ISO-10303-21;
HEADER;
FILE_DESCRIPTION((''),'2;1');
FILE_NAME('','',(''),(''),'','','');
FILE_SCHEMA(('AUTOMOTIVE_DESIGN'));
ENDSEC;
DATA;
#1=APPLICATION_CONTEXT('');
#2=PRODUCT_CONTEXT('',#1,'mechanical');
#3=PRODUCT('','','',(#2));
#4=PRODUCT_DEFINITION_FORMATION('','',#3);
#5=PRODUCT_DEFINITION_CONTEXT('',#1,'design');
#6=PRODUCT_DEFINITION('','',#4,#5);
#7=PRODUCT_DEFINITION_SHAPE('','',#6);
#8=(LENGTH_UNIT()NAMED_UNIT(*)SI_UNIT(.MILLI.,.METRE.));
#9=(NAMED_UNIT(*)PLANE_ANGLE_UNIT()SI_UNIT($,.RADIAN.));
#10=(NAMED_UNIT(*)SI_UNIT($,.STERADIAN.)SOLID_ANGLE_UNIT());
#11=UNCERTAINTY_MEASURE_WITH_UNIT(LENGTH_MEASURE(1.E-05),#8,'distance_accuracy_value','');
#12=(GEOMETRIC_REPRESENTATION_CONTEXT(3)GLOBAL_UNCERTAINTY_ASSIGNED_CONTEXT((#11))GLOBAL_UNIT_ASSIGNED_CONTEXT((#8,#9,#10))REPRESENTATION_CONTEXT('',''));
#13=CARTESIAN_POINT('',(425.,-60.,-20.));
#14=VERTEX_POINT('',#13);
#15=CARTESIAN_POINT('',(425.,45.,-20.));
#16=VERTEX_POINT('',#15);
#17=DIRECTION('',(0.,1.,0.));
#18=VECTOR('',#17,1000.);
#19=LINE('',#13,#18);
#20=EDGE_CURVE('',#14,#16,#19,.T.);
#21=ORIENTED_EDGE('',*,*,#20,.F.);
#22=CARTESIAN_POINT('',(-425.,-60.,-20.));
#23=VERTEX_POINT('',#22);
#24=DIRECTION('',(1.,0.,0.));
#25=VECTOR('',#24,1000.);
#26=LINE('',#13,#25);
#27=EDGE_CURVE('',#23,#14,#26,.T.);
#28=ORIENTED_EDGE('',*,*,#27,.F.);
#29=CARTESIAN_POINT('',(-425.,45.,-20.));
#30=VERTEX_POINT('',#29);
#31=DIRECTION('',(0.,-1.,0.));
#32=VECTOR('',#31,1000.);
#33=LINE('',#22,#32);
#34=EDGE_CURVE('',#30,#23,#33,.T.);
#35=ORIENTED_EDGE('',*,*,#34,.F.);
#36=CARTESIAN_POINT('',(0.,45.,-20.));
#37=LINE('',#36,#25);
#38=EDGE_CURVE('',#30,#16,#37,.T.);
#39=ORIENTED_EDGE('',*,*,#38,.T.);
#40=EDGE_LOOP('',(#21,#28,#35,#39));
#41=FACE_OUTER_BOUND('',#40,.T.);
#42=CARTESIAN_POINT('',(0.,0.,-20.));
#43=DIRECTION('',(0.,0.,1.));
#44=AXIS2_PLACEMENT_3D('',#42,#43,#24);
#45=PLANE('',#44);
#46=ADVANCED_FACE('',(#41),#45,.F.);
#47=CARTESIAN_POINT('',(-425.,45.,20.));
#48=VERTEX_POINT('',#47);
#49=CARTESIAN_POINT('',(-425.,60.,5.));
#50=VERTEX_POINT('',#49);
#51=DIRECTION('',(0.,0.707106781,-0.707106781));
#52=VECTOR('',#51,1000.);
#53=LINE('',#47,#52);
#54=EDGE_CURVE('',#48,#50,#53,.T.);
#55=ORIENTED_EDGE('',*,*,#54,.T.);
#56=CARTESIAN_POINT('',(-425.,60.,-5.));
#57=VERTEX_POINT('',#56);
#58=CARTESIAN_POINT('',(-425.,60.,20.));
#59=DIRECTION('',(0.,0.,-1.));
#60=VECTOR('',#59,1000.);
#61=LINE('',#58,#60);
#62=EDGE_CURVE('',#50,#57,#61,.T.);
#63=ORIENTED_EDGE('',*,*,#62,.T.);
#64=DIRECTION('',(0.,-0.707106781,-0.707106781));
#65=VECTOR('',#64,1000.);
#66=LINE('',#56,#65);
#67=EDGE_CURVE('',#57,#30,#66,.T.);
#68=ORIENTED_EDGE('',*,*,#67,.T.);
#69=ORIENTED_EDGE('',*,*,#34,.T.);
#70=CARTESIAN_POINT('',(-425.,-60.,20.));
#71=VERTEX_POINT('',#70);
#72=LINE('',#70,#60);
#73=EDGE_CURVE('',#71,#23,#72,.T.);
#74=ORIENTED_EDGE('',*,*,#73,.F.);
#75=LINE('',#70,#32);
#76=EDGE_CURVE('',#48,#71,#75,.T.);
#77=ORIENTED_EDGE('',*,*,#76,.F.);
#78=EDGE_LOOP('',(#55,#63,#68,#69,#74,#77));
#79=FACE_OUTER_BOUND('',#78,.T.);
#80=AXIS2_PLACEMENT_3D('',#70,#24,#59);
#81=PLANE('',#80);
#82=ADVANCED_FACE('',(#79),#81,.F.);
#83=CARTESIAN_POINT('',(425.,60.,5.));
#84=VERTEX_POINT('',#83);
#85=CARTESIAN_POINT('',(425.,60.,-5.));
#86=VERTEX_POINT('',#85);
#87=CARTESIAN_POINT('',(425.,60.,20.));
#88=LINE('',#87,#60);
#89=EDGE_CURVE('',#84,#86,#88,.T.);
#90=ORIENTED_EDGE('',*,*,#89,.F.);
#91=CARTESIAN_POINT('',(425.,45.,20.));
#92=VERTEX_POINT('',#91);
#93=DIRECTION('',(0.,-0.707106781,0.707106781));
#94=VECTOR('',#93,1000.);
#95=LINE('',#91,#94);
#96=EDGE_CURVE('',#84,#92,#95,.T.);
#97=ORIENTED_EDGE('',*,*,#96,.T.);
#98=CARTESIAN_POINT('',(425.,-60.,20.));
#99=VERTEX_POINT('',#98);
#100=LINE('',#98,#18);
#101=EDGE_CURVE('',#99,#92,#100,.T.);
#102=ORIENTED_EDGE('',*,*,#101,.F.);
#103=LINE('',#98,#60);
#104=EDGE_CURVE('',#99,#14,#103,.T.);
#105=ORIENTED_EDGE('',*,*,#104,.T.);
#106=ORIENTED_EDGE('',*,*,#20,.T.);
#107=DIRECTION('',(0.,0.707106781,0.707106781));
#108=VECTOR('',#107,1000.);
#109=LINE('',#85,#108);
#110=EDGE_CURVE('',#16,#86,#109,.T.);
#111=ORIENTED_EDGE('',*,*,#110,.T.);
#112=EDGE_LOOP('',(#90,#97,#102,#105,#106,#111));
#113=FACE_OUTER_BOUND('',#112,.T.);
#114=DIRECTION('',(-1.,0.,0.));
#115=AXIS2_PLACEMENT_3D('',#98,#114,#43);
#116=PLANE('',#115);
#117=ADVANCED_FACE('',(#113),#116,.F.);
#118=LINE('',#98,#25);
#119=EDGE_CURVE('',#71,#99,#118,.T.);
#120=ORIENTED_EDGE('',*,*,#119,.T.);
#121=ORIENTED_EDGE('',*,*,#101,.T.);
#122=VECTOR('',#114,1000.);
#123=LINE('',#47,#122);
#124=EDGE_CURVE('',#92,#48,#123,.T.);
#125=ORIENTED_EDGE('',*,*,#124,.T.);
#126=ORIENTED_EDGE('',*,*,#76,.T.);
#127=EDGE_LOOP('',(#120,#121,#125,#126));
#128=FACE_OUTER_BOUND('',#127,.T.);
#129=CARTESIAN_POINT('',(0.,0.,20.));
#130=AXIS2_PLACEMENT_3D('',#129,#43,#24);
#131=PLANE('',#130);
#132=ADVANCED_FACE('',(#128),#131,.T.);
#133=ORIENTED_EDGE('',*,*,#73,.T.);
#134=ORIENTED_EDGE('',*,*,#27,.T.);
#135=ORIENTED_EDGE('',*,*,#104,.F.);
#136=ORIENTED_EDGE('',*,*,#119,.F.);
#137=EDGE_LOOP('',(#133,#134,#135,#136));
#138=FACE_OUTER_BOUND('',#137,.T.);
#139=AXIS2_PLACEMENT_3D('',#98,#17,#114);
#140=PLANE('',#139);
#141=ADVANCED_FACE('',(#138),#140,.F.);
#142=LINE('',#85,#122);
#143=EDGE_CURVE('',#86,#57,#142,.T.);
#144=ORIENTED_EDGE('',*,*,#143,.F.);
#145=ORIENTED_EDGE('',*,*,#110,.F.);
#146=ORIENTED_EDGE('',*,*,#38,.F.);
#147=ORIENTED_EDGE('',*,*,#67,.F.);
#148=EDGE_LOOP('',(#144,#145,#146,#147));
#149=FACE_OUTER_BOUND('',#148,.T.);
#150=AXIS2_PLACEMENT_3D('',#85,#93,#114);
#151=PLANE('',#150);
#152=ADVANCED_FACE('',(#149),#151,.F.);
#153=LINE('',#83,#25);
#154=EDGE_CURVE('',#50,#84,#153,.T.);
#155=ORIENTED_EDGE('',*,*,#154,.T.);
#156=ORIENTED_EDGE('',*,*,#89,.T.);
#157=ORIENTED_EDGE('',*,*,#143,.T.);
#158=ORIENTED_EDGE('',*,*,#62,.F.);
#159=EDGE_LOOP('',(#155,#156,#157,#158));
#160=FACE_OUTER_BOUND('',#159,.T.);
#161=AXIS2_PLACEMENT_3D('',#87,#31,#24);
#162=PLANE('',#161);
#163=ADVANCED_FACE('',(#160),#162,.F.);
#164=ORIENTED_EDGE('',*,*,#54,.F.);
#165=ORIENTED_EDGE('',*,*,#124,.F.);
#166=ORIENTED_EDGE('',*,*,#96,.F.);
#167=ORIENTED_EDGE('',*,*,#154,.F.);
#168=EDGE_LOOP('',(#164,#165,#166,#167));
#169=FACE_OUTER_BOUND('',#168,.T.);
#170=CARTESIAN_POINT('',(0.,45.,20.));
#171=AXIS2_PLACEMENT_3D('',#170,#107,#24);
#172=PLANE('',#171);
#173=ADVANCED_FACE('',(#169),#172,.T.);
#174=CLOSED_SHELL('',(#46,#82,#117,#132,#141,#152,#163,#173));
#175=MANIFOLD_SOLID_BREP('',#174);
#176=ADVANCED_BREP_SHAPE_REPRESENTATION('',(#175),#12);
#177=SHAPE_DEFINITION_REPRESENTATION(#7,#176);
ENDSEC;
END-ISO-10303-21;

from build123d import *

# Parameters (mm, degrees)
SKETCH1_W           = 850
SKETCH1_H           = 120
BOSS_EXTRUDE1_DEPTH = 20
CHAMFER1_SIZE       = 15


with BuildPart() as part:
    # Sketch1 → Boss-Extrude1 (new, symmetric)
    with BuildSketch(Plane.XY):
        Rectangle(SKETCH1_W, SKETCH1_H)
    extrude(amount=BOSS_EXTRUDE1_DEPTH, both=True)

    # Chamfer1
    chamfer1_edges = [part.edges().sort_by_distance(p)[0] for p in [
        (0, 60, 20),
        (0, 60, -20),
    ]]
    chamfer(chamfer1_edges, length=CHAMFER1_SIZE)


solid = part.part
